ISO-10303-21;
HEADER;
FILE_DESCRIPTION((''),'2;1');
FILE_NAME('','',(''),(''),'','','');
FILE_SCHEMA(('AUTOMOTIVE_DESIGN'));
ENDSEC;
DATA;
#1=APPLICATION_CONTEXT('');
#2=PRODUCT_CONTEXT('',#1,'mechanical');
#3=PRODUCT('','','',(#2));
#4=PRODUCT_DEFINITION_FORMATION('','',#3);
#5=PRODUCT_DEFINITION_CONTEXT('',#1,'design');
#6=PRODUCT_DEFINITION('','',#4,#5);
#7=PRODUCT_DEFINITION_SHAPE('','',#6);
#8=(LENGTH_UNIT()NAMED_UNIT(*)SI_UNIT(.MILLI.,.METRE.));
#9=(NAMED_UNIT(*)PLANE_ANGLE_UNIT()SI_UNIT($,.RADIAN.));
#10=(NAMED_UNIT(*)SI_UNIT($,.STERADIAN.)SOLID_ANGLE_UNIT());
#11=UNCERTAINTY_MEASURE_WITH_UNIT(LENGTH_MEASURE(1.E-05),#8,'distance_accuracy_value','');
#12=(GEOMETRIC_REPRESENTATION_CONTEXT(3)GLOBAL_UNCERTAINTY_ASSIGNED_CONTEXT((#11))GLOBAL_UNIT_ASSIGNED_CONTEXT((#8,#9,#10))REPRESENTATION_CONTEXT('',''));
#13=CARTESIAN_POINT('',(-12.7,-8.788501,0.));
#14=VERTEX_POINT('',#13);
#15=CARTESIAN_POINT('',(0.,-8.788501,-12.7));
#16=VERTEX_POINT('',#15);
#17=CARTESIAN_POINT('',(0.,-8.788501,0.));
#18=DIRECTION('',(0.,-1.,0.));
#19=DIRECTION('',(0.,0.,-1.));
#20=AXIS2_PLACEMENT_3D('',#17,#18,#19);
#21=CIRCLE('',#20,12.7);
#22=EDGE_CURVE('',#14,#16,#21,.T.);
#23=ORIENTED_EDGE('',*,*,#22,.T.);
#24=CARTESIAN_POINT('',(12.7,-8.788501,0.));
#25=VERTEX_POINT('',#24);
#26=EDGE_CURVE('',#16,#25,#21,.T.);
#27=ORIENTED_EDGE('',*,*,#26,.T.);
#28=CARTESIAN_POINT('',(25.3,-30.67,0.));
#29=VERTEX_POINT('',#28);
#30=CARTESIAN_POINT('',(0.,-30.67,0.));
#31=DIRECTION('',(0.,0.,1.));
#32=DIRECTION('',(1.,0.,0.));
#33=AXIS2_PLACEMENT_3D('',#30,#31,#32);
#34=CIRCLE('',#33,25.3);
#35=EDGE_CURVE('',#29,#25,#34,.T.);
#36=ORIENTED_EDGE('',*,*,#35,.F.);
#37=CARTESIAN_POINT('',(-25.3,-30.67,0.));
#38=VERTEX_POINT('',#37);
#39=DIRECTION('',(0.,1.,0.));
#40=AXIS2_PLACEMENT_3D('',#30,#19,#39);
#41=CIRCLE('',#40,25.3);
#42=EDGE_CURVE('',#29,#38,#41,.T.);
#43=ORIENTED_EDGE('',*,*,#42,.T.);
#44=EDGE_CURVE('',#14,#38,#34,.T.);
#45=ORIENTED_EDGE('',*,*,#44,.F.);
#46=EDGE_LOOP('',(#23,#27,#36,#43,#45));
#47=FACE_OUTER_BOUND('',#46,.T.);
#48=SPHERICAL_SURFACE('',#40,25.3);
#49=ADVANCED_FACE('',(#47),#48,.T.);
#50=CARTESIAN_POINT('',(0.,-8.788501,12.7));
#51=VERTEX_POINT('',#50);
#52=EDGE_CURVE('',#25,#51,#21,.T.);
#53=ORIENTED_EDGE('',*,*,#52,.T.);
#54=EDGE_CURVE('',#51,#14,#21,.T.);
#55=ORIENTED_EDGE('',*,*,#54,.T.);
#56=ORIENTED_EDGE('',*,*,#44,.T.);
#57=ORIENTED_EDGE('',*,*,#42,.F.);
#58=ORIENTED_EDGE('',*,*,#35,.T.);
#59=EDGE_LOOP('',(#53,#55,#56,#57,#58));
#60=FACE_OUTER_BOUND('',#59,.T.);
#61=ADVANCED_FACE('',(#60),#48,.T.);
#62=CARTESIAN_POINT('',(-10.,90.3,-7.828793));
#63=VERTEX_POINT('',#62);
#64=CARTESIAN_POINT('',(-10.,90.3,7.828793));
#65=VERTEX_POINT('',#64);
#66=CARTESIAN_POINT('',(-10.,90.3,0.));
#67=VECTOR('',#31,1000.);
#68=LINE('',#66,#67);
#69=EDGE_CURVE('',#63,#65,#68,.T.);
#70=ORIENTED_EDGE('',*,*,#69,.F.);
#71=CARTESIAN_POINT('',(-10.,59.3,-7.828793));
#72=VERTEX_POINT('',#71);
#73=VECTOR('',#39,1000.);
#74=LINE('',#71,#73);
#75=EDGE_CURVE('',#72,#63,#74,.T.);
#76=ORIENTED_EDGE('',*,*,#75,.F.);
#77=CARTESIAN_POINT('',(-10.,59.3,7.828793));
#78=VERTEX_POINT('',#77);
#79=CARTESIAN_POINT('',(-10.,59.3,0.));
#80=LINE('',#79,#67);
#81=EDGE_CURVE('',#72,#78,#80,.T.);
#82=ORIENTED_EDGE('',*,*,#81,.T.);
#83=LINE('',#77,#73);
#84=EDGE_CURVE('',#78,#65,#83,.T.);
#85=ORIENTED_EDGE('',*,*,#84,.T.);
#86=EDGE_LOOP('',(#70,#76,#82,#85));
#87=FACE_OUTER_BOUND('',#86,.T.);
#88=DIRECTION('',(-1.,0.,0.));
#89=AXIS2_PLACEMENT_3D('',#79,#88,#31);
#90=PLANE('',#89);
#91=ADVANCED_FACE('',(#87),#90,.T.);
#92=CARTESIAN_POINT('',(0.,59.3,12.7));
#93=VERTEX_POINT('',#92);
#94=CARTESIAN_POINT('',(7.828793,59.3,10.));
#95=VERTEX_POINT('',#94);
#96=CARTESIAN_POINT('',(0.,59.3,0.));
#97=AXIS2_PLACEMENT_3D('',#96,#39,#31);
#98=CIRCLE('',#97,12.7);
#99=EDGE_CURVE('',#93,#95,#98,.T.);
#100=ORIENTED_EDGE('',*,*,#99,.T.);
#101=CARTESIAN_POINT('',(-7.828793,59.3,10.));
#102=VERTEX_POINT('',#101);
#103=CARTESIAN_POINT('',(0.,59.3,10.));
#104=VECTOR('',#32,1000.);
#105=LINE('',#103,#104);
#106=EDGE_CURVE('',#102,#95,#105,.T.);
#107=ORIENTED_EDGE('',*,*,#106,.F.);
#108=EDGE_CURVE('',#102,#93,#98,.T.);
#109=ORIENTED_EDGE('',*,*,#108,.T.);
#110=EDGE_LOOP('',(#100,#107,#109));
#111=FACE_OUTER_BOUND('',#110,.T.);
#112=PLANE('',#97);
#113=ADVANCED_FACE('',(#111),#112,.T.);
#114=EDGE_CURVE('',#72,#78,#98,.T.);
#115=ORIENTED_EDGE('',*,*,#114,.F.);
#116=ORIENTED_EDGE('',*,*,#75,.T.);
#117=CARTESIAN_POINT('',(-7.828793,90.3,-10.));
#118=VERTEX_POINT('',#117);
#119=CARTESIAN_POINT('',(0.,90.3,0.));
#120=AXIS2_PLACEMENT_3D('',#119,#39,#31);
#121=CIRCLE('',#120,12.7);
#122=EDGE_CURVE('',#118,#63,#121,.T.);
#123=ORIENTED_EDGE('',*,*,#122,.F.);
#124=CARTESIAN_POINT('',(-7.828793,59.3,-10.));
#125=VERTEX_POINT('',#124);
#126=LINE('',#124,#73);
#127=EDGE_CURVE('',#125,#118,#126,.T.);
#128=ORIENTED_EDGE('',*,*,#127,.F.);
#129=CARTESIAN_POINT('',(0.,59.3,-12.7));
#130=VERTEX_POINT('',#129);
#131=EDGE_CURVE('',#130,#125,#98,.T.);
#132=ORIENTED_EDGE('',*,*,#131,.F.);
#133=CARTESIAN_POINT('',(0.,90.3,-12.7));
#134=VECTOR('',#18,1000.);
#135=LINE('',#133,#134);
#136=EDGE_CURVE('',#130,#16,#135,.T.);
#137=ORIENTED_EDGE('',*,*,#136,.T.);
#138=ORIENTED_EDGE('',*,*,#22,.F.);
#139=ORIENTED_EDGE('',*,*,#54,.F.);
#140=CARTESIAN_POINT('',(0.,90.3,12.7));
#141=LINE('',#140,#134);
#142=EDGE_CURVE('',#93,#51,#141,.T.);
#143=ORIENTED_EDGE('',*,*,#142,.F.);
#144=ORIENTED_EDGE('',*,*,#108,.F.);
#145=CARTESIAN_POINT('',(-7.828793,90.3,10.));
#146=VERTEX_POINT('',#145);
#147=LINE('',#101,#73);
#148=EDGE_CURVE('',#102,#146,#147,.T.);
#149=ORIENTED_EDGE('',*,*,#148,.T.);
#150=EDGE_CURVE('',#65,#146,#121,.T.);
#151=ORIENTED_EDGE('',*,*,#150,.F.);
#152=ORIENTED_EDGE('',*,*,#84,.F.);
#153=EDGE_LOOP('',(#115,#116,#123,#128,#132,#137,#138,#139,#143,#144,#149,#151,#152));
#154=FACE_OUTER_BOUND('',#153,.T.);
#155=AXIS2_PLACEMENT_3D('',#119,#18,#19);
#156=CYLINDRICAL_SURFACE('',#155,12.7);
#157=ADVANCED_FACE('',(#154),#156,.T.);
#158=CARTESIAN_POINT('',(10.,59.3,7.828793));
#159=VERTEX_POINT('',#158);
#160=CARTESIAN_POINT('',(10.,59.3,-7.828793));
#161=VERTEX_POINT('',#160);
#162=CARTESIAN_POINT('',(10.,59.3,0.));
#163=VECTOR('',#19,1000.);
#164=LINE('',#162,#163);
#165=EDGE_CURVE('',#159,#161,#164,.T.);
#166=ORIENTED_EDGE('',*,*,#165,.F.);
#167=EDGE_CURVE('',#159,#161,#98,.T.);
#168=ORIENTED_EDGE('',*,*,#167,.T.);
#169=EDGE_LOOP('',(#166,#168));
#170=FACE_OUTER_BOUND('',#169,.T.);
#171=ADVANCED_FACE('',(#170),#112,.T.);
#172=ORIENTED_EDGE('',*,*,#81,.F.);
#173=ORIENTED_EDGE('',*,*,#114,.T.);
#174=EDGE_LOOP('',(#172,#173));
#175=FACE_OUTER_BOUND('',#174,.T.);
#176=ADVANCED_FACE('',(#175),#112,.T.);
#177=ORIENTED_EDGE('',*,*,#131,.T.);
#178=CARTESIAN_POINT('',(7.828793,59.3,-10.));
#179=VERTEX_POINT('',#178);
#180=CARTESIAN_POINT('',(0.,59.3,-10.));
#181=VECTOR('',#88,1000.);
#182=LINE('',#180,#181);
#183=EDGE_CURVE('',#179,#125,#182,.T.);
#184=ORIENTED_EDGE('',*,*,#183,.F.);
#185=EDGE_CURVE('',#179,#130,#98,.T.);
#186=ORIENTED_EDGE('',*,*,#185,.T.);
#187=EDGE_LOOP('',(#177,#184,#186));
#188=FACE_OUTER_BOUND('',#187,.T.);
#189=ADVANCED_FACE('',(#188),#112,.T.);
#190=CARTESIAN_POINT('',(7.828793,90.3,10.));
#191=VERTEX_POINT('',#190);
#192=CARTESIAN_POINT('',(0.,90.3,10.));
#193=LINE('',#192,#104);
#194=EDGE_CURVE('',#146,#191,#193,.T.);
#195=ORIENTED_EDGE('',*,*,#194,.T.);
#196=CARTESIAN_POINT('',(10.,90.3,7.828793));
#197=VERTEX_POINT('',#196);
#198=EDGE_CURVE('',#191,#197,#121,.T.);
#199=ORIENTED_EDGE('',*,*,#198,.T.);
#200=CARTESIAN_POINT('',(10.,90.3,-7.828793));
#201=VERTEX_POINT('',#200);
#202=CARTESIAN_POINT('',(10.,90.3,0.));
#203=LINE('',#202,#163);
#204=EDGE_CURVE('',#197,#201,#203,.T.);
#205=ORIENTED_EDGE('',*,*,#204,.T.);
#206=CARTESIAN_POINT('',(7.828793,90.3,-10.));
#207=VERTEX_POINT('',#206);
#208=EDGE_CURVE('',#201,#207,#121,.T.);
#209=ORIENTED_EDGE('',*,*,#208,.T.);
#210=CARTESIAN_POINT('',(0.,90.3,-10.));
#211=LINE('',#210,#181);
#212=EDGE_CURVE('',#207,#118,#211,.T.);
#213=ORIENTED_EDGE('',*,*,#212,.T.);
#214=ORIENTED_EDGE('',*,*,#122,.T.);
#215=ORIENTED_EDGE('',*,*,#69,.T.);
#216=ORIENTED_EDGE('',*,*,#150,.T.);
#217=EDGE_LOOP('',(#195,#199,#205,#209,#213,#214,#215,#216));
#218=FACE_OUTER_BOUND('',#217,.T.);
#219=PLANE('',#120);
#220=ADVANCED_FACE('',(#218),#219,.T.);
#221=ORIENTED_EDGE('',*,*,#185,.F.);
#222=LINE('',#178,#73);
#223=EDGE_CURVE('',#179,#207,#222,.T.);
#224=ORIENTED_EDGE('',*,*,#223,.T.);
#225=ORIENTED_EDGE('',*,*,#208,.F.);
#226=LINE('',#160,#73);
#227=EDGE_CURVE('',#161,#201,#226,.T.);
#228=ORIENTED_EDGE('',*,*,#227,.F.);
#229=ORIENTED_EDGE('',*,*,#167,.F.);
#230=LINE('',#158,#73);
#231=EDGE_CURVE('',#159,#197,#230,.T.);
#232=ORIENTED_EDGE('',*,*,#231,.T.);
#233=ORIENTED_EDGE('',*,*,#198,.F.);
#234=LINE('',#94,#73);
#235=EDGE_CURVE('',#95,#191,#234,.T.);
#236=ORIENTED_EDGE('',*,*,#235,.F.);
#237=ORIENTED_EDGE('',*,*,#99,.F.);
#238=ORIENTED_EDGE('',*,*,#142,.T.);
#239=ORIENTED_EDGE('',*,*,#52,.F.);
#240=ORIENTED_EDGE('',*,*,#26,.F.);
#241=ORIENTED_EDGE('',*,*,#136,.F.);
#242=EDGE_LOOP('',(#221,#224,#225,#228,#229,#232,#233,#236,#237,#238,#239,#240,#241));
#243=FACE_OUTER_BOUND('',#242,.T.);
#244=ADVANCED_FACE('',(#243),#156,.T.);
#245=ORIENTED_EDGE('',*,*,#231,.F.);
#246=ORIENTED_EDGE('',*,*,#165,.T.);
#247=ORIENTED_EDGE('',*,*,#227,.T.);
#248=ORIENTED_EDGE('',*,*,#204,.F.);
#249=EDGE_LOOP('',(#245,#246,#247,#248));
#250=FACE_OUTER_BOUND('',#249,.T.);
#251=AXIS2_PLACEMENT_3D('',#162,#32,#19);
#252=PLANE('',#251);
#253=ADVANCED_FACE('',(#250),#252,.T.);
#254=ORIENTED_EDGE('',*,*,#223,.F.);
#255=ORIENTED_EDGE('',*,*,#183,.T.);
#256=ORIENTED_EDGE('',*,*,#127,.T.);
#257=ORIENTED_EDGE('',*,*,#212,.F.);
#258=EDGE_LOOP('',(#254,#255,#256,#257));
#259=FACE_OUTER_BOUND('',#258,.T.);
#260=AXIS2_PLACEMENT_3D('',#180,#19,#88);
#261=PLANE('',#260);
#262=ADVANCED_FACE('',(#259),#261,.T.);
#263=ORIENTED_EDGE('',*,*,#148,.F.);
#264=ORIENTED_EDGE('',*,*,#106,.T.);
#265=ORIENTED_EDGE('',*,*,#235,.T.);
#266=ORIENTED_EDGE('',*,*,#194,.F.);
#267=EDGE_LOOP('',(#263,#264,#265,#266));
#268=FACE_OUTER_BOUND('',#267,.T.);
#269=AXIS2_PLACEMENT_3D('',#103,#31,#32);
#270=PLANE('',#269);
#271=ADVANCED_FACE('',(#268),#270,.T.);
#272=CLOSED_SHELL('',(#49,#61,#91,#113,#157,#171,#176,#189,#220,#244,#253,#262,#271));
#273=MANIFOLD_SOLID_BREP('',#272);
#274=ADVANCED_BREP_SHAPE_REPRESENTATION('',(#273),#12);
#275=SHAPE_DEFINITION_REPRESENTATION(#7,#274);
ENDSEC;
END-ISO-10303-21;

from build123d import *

# Parameters (mm, degrees)
STEM_SHAFT_SKETCH_25_4_R     = 12.7
STEM_SHAFT_25_4_DEPTH        = 90.3
DRIVE_START                  = -31
DRIVE_SQUARE_FLATS_CUT_DEPTH = 31
STEM_START                   = 31
STEM_BOSS_SKETCH_R           = 12.7
STEM_BOSS_31MM_DEPTH         = 31


with BuildPart() as part:
    # Stem Shaft Sketch _25.4 → Stem Shaft _25.4 (new body)
    with BuildSketch(Plane(origin=(0, 0, 0), x_dir=(1, 0, 0), z_dir=(0, 1, 0))):
        with Locations(Location((0, 0, 0), (0, 0, 270))):
            Circle(STEM_SHAFT_SKETCH_25_4_R)
    extrude(amount=STEM_SHAFT_25_4_DEPTH)

    # Drive Square Flats Sketch → Drive Square Flats Cut (cut)
    with BuildSketch(Plane(origin=(0, 90.3, 0), x_dir=(1, 0, 0), z_dir=(0, 1, 0)).offset(DRIVE_START)):
        with BuildLine():
            ThreePointArc((-7.82879301, -10), (0, -12.7), (7.82879301, -10))
            Line((7.82879301, -10), (-7.82879301, -10))
        make_face()
        with BuildLine():
            Line((-10, -7.82879301), (-10, 7.82879301))
            ThreePointArc((-10, 7.82879301), (-12.7, 0), (-10, -7.82879301))
        make_face()
        with BuildLine():
            Line((-7.82879301, 10), (7.82879301, 10))
            ThreePointArc((7.82879301, 10), (0, 12.7), (-7.82879301, 10))
        make_face()
        with BuildLine():
            Line((10, 7.82879301), (10, 0))
            Line((10, 0), (10, -7.82879301))
            ThreePointArc((10, -7.82879301), (12.006040147, -4.140652123), (12.7, 0))
            ThreePointArc((12.7, 0), (12.006040147, 4.140652123), (10, 7.82879301))
        make_face()
    extrude(amount=DRIVE_SQUARE_FLATS_CUT_DEPTH, mode=Mode.SUBTRACT)

    # Stem Boss Sketch → Stem Boss 31mm (add)
    with BuildSketch(Plane.XZ.offset(STEM_START)):
        with Locations(Location((0, 0, 0), (0, 0, 270))):
            Circle(STEM_BOSS_SKETCH_R)
    extrude(amount=-STEM_BOSS_31MM_DEPTH)


with BuildPart() as body_2:
    # Ball Profile Sketch → Valve Ball (revolve)
    with BuildSketch(Plane.XY):
        with BuildLine():
            Line((-25.3, -30.67), (25.3, -30.67))
            ThreePointArc((25.3, -30.67), (0, -55.97), (-25.3, -30.67))
        make_face()
    revolve(axis=Axis((-25.3, -30.67, 0), (1, 0, 0)))

    # Combine1: union part
    add(part.part)


solid = body_2.part
